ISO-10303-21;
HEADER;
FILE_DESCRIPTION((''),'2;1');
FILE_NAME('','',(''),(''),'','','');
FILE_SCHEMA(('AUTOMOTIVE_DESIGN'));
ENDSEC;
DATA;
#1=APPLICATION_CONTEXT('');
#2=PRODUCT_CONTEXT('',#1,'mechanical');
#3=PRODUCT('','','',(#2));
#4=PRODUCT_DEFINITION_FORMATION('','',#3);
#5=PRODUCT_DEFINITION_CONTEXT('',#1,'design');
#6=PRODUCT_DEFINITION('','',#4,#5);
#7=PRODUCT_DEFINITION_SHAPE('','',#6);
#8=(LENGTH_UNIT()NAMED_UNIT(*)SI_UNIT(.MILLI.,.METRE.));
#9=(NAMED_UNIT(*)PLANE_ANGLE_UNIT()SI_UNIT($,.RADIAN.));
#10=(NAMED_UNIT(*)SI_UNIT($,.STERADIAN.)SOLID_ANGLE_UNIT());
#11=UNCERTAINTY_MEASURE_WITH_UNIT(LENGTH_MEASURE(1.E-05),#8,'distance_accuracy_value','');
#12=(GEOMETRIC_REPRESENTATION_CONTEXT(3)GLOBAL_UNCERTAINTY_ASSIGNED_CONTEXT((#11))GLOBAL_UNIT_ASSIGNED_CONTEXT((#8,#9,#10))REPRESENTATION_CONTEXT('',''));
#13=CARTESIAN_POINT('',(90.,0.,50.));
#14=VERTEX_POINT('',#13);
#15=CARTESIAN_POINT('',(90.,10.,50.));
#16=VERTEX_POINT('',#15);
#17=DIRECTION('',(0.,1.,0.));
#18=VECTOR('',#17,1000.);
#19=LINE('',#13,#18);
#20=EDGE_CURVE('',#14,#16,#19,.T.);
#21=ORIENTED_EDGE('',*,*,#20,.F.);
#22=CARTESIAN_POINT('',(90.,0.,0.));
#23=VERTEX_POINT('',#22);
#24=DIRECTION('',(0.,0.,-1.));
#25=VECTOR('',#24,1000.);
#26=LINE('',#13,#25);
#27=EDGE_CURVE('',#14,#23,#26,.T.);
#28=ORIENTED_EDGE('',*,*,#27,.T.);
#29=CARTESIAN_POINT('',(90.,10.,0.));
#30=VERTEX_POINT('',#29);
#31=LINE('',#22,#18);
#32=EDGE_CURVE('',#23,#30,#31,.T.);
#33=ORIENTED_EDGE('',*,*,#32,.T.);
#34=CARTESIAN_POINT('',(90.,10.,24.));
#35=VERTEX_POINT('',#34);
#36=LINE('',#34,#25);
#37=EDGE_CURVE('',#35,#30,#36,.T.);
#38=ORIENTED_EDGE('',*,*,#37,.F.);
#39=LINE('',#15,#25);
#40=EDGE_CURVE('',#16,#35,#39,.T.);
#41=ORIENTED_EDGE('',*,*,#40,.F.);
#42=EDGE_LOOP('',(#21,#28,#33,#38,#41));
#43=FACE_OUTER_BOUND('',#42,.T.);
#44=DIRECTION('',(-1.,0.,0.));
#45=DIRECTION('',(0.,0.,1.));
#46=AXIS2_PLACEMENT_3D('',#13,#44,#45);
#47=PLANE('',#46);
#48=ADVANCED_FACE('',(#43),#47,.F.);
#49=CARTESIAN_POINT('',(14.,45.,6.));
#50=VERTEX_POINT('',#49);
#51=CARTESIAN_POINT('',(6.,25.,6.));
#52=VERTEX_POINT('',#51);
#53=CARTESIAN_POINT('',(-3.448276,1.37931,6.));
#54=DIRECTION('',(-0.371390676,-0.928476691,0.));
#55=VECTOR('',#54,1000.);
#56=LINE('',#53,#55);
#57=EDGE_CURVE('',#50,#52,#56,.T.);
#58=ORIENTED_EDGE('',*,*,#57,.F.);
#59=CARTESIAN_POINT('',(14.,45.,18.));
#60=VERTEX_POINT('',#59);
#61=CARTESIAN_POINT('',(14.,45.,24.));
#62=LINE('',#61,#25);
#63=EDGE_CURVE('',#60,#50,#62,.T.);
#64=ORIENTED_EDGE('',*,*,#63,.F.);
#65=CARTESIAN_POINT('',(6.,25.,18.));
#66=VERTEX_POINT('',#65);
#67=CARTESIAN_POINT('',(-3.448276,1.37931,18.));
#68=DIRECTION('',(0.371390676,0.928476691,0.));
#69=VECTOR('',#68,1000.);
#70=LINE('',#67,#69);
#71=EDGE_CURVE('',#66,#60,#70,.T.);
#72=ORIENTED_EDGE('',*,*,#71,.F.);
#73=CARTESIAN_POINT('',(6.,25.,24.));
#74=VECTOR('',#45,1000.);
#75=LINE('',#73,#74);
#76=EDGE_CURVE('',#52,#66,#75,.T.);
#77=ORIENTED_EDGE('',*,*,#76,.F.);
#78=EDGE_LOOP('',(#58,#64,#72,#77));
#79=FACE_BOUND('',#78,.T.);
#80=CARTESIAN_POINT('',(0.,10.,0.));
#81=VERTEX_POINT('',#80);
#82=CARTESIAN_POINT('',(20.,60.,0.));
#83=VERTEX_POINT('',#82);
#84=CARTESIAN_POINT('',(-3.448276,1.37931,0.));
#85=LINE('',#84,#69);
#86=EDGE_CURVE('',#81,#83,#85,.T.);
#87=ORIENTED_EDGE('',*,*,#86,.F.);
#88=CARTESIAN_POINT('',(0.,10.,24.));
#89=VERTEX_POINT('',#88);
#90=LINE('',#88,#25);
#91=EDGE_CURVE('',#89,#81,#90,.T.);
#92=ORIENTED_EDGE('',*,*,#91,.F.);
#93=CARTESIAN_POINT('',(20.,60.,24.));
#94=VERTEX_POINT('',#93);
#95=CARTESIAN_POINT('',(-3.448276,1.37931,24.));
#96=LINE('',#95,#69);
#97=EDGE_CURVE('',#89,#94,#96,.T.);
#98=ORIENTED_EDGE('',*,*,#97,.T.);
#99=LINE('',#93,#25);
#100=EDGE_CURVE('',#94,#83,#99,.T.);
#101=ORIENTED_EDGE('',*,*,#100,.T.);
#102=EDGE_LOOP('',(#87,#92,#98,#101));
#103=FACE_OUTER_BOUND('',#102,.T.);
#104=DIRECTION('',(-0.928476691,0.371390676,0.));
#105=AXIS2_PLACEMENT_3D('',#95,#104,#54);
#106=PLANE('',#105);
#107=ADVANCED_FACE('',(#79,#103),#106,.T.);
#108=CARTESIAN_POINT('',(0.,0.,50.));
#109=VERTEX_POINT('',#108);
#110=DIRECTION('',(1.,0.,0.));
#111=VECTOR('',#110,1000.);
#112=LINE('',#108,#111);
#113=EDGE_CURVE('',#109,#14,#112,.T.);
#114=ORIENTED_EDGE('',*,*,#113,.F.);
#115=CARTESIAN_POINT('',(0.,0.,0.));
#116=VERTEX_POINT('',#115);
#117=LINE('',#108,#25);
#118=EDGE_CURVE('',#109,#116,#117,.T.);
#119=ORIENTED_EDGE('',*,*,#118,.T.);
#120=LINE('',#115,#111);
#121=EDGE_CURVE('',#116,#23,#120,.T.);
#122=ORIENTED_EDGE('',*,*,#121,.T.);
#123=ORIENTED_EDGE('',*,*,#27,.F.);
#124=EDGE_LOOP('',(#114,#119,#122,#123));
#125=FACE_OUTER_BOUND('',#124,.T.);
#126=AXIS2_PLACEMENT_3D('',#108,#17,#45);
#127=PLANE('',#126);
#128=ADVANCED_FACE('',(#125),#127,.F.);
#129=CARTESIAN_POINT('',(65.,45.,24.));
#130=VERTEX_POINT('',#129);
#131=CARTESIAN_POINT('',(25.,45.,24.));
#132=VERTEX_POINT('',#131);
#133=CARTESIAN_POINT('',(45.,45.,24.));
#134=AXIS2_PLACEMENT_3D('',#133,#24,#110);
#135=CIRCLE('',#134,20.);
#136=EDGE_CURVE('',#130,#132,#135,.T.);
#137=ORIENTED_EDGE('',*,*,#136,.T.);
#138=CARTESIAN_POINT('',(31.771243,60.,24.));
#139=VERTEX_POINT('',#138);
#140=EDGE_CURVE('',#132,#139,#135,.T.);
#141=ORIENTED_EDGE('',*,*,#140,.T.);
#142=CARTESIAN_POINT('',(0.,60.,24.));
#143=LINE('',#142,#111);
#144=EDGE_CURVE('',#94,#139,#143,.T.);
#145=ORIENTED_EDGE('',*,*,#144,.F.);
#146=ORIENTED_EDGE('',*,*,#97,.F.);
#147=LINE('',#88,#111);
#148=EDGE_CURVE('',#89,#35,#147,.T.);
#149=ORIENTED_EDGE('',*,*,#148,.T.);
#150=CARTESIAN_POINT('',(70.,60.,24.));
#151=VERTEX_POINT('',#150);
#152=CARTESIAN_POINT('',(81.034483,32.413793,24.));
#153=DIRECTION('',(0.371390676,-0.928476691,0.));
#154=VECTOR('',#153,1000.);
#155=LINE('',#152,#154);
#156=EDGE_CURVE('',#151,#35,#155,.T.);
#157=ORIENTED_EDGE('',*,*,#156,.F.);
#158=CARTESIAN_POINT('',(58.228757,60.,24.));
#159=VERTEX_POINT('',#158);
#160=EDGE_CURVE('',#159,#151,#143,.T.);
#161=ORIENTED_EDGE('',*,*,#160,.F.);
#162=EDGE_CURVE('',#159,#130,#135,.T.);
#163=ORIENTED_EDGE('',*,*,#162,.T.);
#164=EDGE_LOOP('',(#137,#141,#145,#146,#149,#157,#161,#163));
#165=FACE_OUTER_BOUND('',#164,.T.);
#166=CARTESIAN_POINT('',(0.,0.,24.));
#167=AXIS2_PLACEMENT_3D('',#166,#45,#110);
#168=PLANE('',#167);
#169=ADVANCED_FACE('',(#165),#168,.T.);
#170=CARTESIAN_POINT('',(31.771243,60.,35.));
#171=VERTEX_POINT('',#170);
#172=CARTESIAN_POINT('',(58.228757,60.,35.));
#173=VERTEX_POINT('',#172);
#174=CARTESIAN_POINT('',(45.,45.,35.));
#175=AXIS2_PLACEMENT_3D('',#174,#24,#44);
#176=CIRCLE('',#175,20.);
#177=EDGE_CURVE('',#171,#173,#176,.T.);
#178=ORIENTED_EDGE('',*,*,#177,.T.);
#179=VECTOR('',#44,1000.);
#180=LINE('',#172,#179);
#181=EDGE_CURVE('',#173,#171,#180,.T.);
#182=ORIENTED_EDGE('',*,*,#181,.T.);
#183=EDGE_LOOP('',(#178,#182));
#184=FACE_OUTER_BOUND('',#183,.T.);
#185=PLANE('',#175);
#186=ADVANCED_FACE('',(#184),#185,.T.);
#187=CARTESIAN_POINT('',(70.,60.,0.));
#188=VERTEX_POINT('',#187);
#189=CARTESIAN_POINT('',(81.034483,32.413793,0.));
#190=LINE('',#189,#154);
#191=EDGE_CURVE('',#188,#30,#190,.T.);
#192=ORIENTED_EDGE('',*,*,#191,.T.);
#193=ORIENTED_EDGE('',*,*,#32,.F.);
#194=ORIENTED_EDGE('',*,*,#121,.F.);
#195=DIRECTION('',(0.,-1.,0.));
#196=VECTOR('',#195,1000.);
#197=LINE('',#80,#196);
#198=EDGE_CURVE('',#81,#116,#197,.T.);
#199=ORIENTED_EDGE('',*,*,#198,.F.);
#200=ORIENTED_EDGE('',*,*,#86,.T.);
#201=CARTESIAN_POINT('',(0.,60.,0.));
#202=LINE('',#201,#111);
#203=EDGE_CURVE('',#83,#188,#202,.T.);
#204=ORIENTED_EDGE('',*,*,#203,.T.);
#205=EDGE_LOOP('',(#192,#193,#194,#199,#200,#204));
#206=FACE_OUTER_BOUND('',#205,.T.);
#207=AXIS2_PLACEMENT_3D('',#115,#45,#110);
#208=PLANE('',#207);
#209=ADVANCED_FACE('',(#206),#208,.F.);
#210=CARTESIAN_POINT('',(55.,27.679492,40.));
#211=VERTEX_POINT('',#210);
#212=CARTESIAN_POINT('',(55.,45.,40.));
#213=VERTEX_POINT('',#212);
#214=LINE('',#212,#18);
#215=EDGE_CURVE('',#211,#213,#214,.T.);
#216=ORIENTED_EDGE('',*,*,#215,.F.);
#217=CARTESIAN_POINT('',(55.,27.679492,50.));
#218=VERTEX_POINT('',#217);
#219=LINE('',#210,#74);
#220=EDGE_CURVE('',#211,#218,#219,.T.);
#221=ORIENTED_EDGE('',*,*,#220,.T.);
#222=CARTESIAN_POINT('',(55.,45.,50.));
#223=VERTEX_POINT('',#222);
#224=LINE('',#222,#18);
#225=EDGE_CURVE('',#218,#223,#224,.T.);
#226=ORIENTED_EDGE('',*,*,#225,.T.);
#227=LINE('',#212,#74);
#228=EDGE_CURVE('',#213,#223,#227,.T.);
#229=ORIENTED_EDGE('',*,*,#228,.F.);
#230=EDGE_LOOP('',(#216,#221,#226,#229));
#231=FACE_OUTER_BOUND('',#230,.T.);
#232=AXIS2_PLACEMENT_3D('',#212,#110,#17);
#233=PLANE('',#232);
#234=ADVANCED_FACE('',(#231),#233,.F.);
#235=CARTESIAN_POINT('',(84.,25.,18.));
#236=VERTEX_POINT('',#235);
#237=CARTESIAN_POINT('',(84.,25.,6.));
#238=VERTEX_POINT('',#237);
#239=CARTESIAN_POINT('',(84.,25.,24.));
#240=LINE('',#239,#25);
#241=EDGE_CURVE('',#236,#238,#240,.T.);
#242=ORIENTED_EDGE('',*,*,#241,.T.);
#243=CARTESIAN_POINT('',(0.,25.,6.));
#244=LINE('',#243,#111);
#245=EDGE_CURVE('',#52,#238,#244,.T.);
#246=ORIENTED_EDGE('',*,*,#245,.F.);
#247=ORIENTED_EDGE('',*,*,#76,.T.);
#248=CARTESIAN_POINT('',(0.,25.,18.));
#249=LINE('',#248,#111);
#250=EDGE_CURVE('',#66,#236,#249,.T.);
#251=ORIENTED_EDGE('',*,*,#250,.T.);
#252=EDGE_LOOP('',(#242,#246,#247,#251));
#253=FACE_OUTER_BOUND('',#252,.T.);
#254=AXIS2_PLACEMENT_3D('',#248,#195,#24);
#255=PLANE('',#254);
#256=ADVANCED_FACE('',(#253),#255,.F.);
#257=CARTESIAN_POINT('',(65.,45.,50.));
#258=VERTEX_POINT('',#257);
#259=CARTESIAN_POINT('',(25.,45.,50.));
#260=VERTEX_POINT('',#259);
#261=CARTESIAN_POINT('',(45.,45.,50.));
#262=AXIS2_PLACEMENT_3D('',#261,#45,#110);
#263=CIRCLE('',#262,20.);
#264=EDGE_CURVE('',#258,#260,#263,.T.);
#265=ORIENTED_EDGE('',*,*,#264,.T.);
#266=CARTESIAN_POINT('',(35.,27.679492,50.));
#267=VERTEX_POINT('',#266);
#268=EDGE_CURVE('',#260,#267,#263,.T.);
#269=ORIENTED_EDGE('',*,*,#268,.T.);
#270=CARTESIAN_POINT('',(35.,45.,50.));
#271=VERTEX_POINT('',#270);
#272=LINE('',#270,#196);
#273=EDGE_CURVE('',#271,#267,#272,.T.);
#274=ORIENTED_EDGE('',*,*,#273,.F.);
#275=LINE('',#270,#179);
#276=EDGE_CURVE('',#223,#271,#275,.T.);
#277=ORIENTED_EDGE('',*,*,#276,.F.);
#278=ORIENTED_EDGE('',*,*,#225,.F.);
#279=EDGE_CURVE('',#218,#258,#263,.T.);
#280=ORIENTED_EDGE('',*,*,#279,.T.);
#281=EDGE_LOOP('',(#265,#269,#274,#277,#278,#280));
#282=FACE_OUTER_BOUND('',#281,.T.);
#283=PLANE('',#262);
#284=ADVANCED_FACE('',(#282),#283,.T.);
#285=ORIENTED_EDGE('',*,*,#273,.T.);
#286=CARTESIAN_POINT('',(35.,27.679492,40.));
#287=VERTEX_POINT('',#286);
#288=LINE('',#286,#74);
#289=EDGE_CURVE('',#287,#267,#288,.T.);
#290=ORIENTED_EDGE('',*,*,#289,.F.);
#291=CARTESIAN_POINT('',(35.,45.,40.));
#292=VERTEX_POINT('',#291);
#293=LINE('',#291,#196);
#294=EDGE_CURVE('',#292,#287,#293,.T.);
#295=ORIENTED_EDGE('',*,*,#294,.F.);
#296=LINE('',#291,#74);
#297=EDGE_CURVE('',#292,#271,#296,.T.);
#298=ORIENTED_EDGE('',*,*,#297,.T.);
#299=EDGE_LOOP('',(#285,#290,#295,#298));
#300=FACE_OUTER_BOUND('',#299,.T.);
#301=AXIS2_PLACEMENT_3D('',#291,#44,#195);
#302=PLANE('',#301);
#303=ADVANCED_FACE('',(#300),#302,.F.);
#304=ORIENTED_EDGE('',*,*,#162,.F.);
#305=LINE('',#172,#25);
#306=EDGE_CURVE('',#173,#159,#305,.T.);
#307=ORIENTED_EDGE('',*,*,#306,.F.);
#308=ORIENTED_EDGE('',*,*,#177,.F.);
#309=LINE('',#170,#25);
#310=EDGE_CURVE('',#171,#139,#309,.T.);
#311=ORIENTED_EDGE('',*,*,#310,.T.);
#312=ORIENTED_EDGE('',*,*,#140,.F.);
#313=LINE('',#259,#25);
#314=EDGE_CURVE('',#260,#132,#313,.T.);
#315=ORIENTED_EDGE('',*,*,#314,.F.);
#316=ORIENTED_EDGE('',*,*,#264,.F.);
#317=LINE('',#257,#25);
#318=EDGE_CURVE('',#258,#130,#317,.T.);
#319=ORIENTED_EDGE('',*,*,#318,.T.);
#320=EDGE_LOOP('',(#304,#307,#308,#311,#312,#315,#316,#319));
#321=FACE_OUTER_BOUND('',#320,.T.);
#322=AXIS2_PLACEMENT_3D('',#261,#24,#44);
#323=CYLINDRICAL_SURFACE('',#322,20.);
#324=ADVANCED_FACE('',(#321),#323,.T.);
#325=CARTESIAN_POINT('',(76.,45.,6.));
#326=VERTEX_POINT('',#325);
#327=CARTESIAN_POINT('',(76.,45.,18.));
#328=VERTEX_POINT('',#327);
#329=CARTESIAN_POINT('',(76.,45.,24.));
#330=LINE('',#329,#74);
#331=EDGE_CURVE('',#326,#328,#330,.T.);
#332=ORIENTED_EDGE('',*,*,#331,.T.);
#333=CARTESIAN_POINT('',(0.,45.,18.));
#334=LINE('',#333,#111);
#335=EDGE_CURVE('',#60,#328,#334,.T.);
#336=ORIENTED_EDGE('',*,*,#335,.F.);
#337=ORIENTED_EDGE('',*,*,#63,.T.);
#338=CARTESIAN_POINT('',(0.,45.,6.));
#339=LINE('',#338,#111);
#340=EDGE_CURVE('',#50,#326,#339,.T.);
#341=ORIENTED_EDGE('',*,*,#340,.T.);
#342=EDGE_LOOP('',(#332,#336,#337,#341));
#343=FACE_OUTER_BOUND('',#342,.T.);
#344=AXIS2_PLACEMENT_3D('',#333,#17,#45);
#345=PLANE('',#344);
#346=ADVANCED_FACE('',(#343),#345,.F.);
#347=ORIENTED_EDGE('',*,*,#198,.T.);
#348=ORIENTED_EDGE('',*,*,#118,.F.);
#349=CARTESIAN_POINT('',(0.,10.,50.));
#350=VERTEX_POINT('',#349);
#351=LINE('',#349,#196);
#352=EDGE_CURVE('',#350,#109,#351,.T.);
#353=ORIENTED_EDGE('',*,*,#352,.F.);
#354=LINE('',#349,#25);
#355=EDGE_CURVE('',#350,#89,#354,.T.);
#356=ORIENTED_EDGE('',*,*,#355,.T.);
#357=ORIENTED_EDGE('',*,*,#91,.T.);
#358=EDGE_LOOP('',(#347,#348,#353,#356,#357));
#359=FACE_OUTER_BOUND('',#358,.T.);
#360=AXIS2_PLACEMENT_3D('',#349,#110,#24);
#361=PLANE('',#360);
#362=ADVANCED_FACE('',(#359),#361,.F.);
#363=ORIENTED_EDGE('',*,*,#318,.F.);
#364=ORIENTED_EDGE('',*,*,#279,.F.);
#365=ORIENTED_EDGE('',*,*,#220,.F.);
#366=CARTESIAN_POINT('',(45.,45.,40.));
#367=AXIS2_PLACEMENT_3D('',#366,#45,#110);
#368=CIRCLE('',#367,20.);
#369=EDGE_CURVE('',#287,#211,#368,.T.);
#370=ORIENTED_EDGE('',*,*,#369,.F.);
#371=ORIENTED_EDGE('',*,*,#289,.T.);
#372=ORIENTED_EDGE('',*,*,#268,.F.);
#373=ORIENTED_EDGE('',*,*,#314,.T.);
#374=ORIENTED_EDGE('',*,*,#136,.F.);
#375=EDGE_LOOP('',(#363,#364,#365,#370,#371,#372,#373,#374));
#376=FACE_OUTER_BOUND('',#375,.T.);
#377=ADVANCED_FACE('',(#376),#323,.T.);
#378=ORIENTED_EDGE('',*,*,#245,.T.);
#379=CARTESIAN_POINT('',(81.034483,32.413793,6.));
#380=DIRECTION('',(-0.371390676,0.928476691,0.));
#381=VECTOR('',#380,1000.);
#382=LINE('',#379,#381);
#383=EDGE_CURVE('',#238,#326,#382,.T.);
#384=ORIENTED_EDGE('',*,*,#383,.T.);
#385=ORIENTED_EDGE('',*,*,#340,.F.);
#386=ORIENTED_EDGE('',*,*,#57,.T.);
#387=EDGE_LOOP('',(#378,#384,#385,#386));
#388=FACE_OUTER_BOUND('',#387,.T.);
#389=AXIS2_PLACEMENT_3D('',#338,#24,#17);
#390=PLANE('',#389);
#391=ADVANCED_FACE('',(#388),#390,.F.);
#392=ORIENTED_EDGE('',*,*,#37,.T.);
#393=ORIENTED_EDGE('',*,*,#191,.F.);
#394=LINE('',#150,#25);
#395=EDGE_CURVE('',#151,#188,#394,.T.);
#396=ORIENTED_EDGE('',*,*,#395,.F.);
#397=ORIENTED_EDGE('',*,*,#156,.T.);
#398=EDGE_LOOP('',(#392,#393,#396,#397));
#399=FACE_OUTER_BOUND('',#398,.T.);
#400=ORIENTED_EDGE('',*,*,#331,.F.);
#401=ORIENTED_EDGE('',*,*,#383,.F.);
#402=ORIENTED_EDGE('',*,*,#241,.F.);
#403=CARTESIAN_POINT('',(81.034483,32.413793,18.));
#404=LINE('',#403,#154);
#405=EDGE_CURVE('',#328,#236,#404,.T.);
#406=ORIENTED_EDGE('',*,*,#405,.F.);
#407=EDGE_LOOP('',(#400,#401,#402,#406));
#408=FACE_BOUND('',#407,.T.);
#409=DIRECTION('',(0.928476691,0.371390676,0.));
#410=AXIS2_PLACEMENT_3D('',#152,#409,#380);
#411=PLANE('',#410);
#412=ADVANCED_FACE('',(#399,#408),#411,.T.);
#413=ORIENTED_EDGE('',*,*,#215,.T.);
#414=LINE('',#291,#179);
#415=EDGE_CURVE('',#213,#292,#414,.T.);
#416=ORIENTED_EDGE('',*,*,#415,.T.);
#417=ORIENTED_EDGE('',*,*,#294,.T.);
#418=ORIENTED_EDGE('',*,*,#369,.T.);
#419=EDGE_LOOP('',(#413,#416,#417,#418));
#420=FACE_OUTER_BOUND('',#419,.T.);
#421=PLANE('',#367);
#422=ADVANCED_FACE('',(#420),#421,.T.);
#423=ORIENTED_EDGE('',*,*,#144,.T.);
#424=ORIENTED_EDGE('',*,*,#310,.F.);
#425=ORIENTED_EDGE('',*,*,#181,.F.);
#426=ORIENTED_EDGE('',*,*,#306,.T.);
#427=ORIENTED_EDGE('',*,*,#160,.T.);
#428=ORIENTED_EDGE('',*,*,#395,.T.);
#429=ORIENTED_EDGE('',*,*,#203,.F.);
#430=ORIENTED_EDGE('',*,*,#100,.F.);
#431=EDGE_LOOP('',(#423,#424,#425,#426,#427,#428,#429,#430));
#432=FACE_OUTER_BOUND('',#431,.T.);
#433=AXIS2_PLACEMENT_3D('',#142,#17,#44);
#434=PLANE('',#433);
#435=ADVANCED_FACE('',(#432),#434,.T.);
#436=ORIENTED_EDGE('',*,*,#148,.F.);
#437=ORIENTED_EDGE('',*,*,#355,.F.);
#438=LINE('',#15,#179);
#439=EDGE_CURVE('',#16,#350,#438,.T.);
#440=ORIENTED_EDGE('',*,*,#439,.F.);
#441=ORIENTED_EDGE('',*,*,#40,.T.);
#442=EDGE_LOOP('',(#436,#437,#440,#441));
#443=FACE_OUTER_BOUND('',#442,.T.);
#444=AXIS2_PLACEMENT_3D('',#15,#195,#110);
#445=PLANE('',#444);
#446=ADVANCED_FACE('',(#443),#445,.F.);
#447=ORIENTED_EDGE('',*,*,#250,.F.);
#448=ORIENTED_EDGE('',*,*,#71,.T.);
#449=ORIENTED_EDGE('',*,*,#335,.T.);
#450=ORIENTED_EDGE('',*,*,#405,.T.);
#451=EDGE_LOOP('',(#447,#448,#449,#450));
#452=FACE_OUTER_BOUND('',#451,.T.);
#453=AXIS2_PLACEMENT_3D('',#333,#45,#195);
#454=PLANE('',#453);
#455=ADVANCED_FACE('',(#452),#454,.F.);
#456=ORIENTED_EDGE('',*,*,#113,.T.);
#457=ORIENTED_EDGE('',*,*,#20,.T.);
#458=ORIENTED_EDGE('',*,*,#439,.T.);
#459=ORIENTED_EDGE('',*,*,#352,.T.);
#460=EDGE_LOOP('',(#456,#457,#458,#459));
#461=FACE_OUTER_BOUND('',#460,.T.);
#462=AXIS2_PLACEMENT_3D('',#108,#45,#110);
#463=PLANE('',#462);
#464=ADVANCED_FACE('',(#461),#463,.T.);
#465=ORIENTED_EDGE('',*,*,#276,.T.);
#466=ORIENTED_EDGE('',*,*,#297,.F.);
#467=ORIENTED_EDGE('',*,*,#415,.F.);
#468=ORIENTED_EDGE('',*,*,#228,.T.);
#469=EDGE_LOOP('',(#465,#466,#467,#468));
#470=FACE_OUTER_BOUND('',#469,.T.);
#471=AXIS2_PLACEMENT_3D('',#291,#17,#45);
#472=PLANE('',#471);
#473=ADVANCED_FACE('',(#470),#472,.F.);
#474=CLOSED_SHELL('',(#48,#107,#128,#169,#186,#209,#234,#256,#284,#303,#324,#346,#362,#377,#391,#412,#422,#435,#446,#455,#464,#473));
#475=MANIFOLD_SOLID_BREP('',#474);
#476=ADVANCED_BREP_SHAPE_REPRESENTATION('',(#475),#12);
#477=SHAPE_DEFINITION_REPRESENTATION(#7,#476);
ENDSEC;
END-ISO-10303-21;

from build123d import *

# Parameters (mm, degrees)
SUPPORT_UPRIGHT_DEPTH      = 24
BASE_PLATE_SKETCH_W        = 90
BASE_PLATE_SKETCH_H        = 10
BASE_PLATE_DEPTH           = 50
BEARING_BOSS_SKETCH_R      = 20
BEARING_BOSS_40_DEPTH      = 26
BOSS_START                 = -10
BOSS_SLOT_CUT_DEPTH        = 10
BOSS_RECESS_CUT_DEPTH      = 11
UPRIGHT_WINDOW_SKETCH_W    = 12
UPRIGHT_WINDOW_SKETCH_H    = 20
UPRIGHT_WINDOW_12X20_DEPTH = 122.757956619


with BuildPart() as part:
    # Support Upright Sketch → Support Upright (new body)
    with BuildSketch(Plane.XY):
        Polygon((0, 10), (20, 60), (70, 60), (90, 10), align=None)
    extrude(amount=SUPPORT_UPRIGHT_DEPTH)

    # Base Plate Sketch → Base Plate (add)
    with BuildSketch(Plane.XY):
        with Locations((45, 5)):
            Rectangle(BASE_PLATE_SKETCH_W, BASE_PLATE_SKETCH_H)
    extrude(amount=BASE_PLATE_DEPTH)

    # Bearing Boss Sketch → Bearing Boss Ø40 (add)
    with BuildSketch(Plane.XY.offset(24)):
        with Locations(Location((45, 45, 0), (0, 0, 131.409622109))):
            Circle(BEARING_BOSS_SKETCH_R)
    extrude(amount=BEARING_BOSS_40_DEPTH)

    # Boss Slot Sketch → Boss Slot Cut (cut)
    with BuildSketch(Plane.XY.offset(50).offset(BOSS_START)):
        with BuildLine():
            Line((35, 45), (55, 45))
            Line((55, 45), (55, 27.679491924))
            ThreePointArc((55, 27.679491924), (45, 25), (35, 27.679491924))
            Line((35, 27.679491924), (35, 45))
        make_face()
    extrude(amount=BOSS_SLOT_CUT_DEPTH, mode=Mode.SUBTRACT)

    # Boss Recess Sketch → Boss Recess Cut (cut)
    with BuildSketch(Plane(origin=(0, 0, 24), x_dir=(-1, 0, 0), z_dir=(0, 0, -1))):
        with BuildLine():
            Line((-58.228756555, 60), (-31.771243445, 60))
            ThreePointArc((-31.771243445, 60), (-45, 65), (-58.228756555, 60))
        make_face()
    extrude(amount=-BOSS_RECESS_CUT_DEPTH, mode=Mode.SUBTRACT)

    # Upright Window Sketch → Upright Window 12x20 (cut, through all)
    with BuildSketch(Plane(origin=(90, 0, 0), x_dir=(0, 0, -1), z_dir=(1, 0, 0))):
        with Locations((-12, 35)):
            Rectangle(UPRIGHT_WINDOW_SKETCH_W, UPRIGHT_WINDOW_SKETCH_H)
    extrude(amount=-UPRIGHT_WINDOW_12X20_DEPTH, mode=Mode.SUBTRACT)


solid = part.part
